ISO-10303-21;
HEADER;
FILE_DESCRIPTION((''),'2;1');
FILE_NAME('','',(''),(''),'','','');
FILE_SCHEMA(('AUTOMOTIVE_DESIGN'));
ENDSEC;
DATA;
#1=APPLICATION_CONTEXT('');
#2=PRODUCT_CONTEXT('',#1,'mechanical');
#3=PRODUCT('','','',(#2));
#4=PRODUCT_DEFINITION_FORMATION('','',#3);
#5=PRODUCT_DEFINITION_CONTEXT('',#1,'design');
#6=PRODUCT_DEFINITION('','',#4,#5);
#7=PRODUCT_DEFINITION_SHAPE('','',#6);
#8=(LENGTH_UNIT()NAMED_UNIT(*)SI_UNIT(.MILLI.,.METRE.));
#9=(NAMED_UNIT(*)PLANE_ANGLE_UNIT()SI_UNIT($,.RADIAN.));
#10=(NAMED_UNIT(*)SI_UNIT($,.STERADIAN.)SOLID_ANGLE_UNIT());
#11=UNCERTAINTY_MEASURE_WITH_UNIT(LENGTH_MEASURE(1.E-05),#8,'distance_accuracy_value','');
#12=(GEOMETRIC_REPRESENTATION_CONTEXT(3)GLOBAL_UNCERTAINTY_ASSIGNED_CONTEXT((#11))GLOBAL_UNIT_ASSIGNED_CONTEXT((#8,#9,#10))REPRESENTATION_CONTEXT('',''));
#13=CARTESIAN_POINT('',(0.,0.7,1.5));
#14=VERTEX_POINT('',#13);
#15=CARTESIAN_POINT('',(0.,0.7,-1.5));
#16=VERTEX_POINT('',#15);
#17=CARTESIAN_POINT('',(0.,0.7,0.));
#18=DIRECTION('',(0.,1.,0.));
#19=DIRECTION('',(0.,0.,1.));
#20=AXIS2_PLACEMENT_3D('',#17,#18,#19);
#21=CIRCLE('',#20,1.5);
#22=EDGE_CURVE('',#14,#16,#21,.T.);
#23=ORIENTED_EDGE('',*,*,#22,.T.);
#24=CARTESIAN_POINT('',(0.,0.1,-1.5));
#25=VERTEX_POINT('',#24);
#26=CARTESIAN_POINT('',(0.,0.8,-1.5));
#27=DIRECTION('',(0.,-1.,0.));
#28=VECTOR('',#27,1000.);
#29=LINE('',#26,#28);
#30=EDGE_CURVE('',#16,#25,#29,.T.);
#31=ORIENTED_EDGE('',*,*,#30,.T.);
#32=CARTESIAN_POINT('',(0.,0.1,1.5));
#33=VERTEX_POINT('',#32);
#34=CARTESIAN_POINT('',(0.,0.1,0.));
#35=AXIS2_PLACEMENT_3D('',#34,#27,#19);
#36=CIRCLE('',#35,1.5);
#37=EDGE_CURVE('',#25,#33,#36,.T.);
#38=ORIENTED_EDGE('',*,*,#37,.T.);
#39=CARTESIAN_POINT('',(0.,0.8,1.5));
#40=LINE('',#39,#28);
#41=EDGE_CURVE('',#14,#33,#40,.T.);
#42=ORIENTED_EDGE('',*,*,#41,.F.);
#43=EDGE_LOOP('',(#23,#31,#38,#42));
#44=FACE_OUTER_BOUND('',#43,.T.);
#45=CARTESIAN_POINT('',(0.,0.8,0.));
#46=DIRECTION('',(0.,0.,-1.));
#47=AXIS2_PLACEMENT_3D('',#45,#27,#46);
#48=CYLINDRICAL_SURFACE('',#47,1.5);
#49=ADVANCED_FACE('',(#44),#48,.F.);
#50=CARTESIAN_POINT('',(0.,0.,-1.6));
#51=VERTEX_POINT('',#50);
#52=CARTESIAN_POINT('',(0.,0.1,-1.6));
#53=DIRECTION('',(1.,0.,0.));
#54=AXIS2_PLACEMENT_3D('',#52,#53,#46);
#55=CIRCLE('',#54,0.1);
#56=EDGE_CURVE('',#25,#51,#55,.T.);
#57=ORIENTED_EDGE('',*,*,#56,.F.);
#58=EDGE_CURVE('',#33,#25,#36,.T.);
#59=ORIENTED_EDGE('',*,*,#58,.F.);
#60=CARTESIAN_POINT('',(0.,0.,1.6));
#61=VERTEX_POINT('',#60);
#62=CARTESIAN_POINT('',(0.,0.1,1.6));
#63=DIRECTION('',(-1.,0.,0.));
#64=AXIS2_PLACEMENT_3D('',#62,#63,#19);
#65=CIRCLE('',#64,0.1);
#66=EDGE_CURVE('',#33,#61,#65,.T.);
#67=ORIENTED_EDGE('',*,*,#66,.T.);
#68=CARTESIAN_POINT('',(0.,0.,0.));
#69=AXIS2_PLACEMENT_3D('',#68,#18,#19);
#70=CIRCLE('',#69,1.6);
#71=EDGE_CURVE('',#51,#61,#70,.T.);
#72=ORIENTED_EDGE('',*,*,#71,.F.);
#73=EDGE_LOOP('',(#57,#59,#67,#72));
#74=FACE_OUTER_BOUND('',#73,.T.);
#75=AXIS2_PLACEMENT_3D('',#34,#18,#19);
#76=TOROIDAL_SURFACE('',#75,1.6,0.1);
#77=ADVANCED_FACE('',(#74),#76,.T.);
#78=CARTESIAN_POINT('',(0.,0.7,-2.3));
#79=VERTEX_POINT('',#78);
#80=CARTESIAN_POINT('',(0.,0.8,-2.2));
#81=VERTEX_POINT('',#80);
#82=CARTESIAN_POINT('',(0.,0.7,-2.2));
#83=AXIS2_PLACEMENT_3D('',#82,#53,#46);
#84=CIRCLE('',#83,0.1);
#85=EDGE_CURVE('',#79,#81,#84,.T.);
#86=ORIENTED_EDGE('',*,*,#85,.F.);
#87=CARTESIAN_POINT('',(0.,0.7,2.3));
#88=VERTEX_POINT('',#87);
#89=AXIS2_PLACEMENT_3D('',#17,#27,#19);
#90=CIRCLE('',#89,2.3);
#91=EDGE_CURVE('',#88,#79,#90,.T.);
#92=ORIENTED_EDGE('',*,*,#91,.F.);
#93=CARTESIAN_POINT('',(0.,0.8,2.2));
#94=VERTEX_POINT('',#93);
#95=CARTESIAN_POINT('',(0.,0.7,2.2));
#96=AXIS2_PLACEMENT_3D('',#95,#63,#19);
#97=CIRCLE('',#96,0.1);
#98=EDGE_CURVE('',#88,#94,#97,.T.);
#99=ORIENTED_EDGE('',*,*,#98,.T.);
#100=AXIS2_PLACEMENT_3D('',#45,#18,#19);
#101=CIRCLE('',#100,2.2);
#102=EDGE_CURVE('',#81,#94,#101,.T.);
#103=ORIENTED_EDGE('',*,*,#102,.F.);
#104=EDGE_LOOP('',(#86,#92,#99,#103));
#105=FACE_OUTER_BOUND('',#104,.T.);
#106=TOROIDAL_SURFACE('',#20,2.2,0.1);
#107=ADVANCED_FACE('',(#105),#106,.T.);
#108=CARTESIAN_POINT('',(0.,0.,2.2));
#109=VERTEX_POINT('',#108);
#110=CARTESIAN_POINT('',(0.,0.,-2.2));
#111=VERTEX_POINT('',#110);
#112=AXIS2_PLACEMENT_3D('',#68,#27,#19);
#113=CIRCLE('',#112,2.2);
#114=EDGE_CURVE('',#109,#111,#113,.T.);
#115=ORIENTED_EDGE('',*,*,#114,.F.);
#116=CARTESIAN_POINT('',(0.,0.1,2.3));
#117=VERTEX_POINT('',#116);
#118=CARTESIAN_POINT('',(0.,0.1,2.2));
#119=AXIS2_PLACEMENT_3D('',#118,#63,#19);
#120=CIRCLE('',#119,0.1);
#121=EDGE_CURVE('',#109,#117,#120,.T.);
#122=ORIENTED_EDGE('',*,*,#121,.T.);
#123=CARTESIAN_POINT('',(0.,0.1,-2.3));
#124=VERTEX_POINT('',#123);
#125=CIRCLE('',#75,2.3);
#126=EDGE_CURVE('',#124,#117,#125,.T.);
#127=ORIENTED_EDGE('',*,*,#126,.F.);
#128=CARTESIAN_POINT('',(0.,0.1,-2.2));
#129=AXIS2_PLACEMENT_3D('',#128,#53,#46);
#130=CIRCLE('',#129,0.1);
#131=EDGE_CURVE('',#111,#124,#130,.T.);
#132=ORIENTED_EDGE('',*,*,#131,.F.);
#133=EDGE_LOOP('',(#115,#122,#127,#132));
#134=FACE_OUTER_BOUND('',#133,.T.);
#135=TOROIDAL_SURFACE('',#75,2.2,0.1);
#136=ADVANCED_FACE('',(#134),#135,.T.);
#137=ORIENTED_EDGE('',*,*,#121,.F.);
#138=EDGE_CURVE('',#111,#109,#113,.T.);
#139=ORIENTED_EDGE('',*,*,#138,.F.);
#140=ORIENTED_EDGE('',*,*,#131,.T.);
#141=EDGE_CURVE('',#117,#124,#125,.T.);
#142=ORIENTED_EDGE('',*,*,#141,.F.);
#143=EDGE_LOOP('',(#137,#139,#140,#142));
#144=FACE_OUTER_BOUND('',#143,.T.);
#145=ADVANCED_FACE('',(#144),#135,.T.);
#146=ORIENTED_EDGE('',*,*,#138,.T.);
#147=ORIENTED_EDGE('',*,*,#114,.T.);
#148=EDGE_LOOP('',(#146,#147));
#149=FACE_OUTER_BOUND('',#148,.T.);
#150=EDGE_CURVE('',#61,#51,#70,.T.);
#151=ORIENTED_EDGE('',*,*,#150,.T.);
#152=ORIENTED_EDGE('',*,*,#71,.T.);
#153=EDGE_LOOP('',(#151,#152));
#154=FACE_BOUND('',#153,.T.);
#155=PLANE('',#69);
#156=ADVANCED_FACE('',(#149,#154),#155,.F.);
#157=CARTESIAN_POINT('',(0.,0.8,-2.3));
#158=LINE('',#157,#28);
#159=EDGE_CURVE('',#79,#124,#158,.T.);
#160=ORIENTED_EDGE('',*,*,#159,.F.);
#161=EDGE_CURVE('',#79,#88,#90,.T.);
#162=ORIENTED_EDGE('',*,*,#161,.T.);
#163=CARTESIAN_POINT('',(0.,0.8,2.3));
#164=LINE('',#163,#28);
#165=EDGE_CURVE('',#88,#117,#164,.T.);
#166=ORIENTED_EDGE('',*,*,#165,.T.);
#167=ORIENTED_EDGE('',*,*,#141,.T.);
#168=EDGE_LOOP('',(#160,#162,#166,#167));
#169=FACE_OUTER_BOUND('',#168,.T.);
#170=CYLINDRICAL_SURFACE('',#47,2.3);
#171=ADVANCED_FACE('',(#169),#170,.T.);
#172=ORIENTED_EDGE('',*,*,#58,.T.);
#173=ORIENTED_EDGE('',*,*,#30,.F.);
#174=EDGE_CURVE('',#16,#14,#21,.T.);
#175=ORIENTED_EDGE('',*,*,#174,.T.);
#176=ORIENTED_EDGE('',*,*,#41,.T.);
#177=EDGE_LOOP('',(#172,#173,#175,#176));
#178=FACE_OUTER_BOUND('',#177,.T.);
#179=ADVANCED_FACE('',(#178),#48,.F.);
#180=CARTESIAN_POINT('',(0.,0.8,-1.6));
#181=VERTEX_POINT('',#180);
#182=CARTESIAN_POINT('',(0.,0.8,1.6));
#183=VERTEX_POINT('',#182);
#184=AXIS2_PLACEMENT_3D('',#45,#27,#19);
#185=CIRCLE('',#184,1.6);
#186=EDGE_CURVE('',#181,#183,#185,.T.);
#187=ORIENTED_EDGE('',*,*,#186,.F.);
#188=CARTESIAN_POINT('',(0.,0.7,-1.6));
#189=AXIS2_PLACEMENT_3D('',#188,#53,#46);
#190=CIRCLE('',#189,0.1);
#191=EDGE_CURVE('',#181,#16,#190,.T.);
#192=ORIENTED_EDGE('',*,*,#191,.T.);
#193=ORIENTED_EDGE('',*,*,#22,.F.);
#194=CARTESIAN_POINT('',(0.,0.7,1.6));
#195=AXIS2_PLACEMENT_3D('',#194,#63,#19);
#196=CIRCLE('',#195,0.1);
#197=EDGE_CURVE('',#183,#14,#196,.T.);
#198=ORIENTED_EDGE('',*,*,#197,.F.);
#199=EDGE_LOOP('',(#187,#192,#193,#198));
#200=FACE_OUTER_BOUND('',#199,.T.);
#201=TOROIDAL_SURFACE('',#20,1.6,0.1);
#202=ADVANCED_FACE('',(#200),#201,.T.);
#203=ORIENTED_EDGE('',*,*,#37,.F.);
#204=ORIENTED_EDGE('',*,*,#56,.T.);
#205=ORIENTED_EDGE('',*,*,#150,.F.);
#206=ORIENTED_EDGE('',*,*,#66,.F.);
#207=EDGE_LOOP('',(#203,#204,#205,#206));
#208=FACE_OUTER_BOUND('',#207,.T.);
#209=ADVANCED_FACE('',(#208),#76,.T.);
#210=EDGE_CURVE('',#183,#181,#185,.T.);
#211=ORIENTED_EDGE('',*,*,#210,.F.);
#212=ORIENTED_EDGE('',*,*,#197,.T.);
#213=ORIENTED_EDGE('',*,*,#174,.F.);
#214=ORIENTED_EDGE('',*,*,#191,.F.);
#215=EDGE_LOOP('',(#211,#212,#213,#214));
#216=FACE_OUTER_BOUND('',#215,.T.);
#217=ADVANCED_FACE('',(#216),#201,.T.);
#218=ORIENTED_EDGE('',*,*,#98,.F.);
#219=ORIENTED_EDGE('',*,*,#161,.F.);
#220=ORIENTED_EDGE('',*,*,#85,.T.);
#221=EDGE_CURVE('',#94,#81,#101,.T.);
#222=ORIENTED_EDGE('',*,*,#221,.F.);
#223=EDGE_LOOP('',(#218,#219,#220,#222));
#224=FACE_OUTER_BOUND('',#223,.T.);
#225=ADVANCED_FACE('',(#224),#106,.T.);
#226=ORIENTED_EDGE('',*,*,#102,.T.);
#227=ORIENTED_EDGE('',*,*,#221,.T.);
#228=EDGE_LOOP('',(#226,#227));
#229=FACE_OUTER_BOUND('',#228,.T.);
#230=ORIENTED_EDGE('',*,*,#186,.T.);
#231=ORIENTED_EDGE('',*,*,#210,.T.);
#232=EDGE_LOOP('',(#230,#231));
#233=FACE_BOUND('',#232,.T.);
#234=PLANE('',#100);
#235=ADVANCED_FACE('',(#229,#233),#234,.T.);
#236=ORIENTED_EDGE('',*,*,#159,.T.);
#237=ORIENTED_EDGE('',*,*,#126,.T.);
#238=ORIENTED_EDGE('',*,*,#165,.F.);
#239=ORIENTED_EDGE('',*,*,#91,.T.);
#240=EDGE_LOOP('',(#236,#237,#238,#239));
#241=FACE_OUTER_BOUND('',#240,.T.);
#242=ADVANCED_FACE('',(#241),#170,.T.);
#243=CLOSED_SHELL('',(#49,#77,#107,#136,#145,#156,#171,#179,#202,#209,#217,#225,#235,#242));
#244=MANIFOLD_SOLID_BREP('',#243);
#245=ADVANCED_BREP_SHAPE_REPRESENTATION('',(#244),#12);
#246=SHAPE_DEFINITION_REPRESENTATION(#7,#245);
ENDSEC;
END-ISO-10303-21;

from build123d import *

# Parameters (mm, degrees)
SKETCH_1_R      = 2.3
SKETCH_1_R_2    = 1.5
EXTRUDE_1_DEPTH = 0.8
FILLET_1_R      = 0.1


with BuildPart() as part:
    # 草图1 → 凸台-拉伸1 (new body)
    with BuildSketch(Plane(origin=(0, 0, 0), x_dir=(1, 0, 0), z_dir=(0, 1, 0))):
        with Locations(Location((0, 0, 0), (0, 0, 270))):
            Circle(SKETCH_1_R)
        with Locations(Location((0, 0, 0), (0, 0, 270))):
            Circle(SKETCH_1_R_2, mode=Mode.SUBTRACT)
    extrude(amount=EXTRUDE_1_DEPTH)

    # 圆角1
    fillet_1_edges = [part.edges().sort_by_distance(p)[0] for p in [
        (0, 0, -2.3),
        (0, 0.8, -2.3),
        (0, 0, -1.5),
        (0, 0.8, -1.5),
    ]]
    fillet(fillet_1_edges, radius=FILLET_1_R)


solid = part.part
